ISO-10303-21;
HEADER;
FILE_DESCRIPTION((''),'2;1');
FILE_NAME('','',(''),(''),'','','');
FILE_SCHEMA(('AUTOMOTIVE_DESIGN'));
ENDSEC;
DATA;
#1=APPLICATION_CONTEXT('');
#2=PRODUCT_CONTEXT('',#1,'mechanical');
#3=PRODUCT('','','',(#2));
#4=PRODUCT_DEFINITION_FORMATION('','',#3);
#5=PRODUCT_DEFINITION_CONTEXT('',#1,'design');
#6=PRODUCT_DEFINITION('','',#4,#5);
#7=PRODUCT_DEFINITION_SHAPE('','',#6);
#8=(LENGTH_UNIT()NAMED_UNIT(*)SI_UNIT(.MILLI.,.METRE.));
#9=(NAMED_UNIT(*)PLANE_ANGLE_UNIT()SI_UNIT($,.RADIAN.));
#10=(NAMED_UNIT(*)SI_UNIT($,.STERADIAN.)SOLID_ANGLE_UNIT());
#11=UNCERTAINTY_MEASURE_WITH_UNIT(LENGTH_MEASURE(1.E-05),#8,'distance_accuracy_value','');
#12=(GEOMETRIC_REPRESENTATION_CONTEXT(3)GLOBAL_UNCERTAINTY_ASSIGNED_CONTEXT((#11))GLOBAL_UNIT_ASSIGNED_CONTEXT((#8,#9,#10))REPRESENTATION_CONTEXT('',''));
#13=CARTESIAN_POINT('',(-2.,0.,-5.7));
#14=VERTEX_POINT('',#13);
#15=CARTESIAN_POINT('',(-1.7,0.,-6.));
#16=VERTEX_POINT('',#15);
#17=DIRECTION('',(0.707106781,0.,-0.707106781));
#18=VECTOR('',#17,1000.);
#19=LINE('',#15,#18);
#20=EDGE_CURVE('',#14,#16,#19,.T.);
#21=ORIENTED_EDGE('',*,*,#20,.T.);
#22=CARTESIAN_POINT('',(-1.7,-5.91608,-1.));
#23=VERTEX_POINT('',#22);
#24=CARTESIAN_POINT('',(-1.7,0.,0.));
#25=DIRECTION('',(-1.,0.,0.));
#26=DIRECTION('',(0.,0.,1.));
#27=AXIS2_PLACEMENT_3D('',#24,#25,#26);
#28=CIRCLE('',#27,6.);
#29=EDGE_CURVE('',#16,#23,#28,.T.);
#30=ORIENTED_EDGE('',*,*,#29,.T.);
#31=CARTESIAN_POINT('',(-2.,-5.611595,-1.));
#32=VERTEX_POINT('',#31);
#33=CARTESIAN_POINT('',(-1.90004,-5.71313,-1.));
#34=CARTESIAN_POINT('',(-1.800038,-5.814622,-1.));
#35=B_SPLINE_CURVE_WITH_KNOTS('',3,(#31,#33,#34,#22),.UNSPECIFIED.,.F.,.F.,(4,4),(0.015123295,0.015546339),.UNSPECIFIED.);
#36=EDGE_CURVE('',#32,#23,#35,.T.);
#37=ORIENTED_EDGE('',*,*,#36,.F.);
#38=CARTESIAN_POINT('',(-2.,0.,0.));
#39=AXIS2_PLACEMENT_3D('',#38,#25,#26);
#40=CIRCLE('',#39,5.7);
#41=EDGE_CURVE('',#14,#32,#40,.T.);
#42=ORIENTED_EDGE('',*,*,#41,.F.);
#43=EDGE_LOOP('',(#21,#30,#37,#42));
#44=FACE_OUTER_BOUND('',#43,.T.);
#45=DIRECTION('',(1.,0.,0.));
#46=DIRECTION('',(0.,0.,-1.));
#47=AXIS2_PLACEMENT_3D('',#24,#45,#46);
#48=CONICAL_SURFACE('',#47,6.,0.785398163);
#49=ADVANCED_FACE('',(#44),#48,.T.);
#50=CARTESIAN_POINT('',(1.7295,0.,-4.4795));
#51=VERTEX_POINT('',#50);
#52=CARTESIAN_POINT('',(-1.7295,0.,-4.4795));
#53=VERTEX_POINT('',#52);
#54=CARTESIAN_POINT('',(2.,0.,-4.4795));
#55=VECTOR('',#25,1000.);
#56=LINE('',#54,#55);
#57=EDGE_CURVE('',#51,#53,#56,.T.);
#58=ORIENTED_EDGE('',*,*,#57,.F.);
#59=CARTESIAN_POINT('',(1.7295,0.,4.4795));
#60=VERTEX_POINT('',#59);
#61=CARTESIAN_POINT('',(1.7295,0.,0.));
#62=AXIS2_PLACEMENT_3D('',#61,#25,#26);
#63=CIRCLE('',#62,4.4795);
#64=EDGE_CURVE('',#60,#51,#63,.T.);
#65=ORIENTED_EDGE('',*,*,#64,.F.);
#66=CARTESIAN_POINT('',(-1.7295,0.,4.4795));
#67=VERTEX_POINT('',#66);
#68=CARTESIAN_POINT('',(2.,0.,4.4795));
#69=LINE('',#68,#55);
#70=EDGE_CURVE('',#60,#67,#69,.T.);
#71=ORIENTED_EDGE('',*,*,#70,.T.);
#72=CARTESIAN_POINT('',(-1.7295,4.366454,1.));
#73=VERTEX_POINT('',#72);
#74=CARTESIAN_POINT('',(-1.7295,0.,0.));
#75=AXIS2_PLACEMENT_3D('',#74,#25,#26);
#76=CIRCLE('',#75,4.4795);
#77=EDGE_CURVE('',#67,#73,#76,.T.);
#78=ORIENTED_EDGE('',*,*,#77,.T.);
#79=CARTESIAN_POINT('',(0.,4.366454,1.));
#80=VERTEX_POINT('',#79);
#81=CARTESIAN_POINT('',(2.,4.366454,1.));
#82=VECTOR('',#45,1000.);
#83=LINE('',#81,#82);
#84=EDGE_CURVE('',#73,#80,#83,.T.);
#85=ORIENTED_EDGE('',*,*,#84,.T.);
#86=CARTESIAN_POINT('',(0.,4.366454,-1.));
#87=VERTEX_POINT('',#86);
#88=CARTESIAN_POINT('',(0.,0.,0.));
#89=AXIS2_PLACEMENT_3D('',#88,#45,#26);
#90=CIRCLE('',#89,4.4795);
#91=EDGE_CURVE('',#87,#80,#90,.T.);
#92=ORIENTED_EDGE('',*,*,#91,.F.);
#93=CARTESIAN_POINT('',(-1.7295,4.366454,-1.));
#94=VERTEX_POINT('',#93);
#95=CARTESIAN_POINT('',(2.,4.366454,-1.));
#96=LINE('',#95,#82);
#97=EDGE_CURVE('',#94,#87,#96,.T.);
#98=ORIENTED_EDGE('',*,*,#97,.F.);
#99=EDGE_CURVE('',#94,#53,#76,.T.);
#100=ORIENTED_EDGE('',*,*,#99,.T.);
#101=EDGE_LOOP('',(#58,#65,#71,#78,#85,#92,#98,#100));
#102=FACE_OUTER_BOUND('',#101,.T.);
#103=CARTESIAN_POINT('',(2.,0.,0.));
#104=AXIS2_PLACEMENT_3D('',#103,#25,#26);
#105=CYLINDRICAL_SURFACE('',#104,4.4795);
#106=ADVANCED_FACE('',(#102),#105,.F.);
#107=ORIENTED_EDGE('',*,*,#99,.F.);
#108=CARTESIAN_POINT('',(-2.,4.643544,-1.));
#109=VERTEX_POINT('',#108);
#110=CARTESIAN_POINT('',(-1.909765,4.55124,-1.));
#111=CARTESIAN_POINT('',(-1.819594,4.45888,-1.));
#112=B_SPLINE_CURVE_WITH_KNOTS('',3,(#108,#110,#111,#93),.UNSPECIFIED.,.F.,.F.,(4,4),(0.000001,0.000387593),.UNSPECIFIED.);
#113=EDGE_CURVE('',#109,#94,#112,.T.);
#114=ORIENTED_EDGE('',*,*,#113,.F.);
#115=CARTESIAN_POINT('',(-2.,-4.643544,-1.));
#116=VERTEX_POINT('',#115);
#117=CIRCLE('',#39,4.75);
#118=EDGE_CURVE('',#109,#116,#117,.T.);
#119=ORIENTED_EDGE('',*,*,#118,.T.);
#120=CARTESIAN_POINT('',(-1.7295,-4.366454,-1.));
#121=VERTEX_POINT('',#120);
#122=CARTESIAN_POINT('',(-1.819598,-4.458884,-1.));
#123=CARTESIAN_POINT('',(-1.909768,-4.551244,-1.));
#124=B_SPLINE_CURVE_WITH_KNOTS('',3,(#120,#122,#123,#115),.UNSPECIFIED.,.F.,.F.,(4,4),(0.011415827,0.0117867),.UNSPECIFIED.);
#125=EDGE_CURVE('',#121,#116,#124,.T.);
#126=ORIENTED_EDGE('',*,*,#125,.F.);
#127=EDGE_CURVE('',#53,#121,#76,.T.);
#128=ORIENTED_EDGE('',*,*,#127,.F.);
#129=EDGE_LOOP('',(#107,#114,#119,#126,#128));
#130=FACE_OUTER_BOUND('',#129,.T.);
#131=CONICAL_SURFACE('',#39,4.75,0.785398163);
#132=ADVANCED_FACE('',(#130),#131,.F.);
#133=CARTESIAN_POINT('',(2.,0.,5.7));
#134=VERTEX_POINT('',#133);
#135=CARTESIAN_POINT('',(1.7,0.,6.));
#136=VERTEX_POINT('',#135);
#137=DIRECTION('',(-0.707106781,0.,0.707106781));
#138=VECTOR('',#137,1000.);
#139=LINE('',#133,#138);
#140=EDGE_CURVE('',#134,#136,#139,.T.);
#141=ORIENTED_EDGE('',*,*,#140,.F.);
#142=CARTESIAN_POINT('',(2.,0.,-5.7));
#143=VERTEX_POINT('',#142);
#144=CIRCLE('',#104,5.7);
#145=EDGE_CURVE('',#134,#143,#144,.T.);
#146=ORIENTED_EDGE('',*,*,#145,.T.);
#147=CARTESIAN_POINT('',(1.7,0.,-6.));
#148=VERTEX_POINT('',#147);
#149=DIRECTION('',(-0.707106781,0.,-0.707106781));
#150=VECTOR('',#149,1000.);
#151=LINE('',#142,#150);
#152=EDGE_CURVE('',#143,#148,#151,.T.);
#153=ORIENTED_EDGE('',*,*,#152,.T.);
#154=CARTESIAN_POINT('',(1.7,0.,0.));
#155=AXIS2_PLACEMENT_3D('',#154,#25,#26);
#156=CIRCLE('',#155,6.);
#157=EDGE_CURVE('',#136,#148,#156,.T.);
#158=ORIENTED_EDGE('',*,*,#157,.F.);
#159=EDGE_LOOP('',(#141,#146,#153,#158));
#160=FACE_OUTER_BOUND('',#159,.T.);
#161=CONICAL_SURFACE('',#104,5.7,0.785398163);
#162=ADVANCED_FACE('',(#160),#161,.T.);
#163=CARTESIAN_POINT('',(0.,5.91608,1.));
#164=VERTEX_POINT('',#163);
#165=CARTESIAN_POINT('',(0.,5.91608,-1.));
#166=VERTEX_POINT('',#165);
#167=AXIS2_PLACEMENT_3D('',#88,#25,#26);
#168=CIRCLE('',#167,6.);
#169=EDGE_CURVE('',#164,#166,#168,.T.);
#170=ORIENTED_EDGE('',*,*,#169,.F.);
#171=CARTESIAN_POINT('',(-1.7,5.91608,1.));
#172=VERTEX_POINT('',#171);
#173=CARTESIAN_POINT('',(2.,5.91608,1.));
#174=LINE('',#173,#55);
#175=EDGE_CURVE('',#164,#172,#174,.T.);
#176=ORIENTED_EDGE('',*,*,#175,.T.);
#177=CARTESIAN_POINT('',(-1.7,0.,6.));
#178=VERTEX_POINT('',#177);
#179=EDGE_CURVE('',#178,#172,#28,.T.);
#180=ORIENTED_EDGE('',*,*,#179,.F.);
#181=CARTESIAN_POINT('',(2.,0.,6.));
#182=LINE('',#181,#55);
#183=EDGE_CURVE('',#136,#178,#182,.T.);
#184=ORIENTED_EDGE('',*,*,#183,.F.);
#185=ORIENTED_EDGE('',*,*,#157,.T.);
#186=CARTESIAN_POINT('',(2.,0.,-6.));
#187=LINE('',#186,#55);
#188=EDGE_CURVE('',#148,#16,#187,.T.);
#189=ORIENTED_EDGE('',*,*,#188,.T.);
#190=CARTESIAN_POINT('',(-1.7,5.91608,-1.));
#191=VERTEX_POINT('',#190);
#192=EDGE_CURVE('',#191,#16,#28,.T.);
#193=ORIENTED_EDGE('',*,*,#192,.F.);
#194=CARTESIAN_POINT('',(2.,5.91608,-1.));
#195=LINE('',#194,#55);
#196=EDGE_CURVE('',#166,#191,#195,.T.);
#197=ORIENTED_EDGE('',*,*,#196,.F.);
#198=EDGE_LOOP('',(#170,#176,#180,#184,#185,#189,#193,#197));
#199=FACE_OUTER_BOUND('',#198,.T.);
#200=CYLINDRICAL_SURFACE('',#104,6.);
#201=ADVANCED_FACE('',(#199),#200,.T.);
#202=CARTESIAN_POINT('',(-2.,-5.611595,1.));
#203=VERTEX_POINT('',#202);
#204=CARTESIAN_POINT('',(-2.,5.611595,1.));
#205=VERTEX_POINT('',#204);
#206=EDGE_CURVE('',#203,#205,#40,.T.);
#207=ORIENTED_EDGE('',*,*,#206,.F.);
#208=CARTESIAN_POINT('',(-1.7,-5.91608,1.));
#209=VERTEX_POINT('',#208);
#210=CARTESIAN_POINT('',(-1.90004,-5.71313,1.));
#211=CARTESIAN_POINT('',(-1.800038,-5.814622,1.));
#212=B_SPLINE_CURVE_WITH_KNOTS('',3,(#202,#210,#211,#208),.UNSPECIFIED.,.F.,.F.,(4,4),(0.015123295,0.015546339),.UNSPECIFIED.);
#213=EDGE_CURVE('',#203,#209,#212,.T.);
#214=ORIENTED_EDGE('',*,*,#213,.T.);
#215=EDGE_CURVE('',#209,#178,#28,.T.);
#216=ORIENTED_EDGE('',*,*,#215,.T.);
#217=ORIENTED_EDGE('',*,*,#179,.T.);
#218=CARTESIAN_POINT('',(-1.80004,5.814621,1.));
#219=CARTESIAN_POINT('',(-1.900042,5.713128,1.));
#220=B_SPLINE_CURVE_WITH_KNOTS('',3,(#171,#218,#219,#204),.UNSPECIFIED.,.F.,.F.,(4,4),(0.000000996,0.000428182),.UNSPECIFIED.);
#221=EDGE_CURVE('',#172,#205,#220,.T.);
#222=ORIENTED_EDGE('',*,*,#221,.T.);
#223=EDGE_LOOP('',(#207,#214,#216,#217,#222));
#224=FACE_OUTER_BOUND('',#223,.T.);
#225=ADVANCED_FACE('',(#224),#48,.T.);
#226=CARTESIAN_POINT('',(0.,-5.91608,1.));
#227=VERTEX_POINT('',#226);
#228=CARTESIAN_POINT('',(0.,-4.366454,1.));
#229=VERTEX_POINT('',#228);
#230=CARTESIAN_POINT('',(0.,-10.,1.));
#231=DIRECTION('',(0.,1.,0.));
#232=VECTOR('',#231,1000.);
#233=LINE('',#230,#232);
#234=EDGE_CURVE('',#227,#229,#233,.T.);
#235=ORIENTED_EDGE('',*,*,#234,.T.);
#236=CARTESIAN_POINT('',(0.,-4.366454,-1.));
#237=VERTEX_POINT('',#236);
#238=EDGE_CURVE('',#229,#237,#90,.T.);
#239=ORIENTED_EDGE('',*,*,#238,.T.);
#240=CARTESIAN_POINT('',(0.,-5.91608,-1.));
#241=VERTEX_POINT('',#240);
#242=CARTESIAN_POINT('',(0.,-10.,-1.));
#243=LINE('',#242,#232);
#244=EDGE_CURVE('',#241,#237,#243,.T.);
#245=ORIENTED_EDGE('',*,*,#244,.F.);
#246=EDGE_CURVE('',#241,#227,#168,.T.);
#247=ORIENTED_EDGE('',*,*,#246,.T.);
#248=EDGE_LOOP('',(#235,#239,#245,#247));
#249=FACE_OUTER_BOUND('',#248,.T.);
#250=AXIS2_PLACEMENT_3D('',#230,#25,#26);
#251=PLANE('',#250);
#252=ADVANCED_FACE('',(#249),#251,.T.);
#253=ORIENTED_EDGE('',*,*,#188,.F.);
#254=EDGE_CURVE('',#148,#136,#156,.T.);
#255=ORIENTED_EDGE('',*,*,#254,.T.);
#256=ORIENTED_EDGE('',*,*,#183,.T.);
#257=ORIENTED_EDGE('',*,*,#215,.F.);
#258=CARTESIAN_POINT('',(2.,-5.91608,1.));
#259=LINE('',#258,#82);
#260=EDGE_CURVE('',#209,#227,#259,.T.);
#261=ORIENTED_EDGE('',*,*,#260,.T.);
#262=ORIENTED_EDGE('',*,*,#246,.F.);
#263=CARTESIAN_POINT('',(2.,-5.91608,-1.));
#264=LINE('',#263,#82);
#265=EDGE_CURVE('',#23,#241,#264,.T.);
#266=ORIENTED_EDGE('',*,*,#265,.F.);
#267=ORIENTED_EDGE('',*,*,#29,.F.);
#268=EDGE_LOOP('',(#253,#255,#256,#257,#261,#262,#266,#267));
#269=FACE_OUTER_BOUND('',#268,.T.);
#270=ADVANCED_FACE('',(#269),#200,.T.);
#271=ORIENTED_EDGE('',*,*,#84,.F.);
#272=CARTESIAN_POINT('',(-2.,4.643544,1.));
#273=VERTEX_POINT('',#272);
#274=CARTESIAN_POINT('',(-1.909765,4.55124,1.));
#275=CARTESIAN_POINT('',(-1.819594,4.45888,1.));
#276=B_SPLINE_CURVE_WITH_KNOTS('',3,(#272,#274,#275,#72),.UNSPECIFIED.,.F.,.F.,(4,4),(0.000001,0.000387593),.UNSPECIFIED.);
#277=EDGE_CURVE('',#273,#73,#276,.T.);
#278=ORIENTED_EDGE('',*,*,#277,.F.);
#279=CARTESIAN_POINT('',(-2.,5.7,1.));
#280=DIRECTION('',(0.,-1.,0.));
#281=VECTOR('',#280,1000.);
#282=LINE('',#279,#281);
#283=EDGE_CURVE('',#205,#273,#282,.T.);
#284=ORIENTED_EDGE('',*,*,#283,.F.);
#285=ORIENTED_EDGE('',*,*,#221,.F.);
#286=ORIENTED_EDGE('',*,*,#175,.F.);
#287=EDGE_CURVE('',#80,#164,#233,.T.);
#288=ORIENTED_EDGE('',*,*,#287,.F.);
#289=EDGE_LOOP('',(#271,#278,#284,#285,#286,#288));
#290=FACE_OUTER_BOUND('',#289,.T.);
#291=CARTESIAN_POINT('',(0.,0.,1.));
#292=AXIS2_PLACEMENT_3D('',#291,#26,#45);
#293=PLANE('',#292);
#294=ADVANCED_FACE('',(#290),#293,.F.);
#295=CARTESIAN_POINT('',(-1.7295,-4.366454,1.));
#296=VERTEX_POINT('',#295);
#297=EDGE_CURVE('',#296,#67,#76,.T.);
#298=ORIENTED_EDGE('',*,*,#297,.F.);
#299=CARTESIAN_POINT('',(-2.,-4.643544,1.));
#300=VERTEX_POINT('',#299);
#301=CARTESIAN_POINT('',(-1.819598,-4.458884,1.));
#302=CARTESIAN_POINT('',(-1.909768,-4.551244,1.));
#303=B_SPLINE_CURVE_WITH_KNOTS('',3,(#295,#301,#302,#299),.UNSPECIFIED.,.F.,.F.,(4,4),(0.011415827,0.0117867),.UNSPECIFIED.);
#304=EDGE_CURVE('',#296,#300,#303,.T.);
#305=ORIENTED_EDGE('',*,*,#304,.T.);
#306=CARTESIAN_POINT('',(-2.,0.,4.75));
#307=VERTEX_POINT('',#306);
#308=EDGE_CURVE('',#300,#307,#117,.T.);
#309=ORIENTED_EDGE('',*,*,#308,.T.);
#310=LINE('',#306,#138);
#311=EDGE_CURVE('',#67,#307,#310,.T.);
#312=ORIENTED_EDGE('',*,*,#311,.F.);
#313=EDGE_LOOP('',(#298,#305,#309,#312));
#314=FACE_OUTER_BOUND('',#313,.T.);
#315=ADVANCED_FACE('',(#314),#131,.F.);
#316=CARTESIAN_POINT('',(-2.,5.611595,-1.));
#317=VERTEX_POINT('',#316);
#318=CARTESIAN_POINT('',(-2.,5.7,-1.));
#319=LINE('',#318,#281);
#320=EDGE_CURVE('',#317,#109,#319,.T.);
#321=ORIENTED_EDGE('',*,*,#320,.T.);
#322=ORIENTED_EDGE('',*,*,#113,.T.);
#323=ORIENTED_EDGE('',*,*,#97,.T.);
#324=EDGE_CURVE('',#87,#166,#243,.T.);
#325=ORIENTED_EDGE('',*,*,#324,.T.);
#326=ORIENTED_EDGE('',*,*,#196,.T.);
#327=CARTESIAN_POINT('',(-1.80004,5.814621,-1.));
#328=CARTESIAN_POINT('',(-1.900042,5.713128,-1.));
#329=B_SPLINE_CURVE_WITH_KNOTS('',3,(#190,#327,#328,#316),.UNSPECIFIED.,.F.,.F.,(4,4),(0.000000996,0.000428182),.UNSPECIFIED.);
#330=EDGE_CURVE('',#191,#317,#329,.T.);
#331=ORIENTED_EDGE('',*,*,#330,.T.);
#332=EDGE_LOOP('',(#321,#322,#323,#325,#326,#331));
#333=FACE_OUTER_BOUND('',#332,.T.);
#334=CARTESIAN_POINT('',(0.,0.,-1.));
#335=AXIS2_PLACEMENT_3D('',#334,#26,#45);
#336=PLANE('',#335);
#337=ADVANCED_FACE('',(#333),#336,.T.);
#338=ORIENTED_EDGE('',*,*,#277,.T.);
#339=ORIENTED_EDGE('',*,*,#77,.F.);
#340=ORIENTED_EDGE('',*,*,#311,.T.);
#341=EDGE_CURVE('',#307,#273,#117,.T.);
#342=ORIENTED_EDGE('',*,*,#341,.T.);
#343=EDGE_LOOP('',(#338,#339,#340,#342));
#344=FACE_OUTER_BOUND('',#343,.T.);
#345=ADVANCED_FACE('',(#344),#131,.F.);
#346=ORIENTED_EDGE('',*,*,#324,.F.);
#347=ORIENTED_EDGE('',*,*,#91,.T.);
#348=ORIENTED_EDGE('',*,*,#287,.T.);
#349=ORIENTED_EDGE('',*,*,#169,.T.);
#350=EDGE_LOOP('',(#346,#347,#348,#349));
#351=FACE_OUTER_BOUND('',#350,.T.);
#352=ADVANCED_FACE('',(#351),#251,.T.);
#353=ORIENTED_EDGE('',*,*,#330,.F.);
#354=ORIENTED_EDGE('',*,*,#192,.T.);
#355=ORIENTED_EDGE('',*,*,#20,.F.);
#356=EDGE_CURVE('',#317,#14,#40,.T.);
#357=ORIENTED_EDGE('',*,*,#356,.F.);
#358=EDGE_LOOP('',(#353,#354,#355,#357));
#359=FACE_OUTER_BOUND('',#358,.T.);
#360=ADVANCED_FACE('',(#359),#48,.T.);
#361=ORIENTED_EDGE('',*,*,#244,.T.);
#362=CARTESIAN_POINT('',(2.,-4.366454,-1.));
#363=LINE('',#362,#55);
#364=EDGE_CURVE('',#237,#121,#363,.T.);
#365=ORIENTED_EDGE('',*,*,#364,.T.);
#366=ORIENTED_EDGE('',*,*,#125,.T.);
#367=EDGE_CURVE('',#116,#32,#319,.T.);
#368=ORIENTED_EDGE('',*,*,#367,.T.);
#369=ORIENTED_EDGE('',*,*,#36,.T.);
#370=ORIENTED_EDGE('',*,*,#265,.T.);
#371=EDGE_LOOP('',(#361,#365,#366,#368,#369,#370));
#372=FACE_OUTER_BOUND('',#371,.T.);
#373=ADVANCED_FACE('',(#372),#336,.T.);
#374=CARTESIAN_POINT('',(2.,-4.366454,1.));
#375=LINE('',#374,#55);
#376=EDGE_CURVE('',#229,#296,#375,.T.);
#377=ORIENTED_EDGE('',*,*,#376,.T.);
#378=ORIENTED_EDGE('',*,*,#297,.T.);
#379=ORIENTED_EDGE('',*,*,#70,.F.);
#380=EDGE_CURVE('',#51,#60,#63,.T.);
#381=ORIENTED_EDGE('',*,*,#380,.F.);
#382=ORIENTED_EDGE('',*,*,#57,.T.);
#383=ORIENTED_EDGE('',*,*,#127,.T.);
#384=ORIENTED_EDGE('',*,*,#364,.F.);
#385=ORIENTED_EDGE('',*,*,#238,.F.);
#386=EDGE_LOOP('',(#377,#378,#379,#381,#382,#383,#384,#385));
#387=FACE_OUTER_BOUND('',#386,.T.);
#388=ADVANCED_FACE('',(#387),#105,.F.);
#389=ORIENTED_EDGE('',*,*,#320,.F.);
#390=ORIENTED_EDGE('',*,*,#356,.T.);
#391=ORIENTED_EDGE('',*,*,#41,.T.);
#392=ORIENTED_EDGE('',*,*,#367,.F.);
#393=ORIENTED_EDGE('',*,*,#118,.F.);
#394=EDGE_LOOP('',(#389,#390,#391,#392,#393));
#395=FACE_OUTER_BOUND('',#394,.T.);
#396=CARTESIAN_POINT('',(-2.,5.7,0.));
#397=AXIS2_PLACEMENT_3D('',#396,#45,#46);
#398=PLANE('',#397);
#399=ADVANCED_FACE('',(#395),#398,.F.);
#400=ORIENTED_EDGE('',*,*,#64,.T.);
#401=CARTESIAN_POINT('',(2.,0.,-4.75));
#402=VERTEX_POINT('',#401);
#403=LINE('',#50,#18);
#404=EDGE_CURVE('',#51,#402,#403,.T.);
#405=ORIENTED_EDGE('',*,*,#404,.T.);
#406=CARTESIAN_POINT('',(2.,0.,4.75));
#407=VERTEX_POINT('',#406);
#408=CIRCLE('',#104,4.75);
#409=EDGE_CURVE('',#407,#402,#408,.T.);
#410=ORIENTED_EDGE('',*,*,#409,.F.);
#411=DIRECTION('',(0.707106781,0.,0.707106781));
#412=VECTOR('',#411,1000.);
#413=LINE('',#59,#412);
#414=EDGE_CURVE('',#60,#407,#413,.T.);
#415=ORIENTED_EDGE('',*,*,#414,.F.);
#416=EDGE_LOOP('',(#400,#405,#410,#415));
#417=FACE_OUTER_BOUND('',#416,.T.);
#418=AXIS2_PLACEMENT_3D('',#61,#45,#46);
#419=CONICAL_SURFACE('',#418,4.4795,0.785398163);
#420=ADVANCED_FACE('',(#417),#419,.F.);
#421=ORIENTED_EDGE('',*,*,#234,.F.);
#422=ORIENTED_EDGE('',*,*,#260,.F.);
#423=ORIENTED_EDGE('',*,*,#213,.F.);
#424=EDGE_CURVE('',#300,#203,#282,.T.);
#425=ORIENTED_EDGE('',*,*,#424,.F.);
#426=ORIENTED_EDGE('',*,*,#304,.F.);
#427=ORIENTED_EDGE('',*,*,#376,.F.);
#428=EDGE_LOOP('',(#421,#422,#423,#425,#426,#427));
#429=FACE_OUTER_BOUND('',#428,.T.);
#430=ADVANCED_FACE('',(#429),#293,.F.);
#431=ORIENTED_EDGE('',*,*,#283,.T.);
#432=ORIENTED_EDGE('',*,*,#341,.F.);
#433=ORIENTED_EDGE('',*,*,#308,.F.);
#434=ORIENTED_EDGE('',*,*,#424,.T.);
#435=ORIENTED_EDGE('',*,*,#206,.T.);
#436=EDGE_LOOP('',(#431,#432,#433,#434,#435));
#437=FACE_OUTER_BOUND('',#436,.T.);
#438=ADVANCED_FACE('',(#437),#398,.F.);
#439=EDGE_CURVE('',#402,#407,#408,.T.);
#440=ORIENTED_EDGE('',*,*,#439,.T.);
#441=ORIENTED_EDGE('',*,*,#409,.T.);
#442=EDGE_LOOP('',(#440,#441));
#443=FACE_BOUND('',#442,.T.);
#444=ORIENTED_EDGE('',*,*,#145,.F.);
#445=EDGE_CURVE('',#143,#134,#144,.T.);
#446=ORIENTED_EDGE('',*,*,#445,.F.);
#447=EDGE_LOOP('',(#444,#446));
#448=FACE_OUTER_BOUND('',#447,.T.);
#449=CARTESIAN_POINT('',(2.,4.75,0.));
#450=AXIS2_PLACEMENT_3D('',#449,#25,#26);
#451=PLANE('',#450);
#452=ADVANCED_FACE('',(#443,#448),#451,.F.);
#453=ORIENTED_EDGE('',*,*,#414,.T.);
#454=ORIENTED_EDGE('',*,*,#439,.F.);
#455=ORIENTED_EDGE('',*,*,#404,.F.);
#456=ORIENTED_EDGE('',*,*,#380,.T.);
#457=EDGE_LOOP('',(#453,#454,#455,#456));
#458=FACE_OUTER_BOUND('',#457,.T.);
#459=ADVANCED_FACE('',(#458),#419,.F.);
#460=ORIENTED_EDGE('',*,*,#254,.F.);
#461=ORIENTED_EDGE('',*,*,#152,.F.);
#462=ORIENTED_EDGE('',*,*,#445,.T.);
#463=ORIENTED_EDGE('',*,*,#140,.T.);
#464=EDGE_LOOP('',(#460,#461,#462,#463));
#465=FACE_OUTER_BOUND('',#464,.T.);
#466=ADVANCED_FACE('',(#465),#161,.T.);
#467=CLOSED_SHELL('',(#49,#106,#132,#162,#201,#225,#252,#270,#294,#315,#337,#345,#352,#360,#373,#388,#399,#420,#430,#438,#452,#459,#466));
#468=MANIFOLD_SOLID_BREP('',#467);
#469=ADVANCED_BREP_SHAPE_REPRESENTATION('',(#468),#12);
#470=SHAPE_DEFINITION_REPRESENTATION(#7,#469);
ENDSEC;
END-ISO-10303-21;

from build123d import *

# Parameters (mm, degrees)
CUT_EXTRUDE_1_DEPTH      = 1
CUT_EXTRUDE_1_DEPTH_BACK = 1
SKETCH_2_W               = 5
SKETCH_2_H               = 20


with BuildPart() as part:
    # 草图1 → 旋转1 (revolve)
    with BuildSketch(Plane.XY, mode=Mode.PRIVATE) as revolve_1_sk:
        Polygon((-2, 4.75), (-1.7295, 4.4795), (1.7295, 4.4795), (2, 4.75), (2, 5.7), (1.7, 6), (-1.7, 6), (-2, 5.7), align=None)
    revolve(revolve_1_sk.sketch.rotate(Axis((2, 0, 0), (-1, 0, 0)), 270), axis=Axis((2, 0, 0), (-1, 0, 0)))

    # 草图2 → 切除-拉伸1 (cut, two sides: drawn at the far end of the back side and taken through both)
    with BuildSketch(Plane.XY.offset(-CUT_EXTRUDE_1_DEPTH_BACK)):
        with Locations((-2.5, 0)):
            Rectangle(SKETCH_2_W, SKETCH_2_H)
    extrude(amount=CUT_EXTRUDE_1_DEPTH + CUT_EXTRUDE_1_DEPTH_BACK, mode=Mode.SUBTRACT)


solid = part.part
